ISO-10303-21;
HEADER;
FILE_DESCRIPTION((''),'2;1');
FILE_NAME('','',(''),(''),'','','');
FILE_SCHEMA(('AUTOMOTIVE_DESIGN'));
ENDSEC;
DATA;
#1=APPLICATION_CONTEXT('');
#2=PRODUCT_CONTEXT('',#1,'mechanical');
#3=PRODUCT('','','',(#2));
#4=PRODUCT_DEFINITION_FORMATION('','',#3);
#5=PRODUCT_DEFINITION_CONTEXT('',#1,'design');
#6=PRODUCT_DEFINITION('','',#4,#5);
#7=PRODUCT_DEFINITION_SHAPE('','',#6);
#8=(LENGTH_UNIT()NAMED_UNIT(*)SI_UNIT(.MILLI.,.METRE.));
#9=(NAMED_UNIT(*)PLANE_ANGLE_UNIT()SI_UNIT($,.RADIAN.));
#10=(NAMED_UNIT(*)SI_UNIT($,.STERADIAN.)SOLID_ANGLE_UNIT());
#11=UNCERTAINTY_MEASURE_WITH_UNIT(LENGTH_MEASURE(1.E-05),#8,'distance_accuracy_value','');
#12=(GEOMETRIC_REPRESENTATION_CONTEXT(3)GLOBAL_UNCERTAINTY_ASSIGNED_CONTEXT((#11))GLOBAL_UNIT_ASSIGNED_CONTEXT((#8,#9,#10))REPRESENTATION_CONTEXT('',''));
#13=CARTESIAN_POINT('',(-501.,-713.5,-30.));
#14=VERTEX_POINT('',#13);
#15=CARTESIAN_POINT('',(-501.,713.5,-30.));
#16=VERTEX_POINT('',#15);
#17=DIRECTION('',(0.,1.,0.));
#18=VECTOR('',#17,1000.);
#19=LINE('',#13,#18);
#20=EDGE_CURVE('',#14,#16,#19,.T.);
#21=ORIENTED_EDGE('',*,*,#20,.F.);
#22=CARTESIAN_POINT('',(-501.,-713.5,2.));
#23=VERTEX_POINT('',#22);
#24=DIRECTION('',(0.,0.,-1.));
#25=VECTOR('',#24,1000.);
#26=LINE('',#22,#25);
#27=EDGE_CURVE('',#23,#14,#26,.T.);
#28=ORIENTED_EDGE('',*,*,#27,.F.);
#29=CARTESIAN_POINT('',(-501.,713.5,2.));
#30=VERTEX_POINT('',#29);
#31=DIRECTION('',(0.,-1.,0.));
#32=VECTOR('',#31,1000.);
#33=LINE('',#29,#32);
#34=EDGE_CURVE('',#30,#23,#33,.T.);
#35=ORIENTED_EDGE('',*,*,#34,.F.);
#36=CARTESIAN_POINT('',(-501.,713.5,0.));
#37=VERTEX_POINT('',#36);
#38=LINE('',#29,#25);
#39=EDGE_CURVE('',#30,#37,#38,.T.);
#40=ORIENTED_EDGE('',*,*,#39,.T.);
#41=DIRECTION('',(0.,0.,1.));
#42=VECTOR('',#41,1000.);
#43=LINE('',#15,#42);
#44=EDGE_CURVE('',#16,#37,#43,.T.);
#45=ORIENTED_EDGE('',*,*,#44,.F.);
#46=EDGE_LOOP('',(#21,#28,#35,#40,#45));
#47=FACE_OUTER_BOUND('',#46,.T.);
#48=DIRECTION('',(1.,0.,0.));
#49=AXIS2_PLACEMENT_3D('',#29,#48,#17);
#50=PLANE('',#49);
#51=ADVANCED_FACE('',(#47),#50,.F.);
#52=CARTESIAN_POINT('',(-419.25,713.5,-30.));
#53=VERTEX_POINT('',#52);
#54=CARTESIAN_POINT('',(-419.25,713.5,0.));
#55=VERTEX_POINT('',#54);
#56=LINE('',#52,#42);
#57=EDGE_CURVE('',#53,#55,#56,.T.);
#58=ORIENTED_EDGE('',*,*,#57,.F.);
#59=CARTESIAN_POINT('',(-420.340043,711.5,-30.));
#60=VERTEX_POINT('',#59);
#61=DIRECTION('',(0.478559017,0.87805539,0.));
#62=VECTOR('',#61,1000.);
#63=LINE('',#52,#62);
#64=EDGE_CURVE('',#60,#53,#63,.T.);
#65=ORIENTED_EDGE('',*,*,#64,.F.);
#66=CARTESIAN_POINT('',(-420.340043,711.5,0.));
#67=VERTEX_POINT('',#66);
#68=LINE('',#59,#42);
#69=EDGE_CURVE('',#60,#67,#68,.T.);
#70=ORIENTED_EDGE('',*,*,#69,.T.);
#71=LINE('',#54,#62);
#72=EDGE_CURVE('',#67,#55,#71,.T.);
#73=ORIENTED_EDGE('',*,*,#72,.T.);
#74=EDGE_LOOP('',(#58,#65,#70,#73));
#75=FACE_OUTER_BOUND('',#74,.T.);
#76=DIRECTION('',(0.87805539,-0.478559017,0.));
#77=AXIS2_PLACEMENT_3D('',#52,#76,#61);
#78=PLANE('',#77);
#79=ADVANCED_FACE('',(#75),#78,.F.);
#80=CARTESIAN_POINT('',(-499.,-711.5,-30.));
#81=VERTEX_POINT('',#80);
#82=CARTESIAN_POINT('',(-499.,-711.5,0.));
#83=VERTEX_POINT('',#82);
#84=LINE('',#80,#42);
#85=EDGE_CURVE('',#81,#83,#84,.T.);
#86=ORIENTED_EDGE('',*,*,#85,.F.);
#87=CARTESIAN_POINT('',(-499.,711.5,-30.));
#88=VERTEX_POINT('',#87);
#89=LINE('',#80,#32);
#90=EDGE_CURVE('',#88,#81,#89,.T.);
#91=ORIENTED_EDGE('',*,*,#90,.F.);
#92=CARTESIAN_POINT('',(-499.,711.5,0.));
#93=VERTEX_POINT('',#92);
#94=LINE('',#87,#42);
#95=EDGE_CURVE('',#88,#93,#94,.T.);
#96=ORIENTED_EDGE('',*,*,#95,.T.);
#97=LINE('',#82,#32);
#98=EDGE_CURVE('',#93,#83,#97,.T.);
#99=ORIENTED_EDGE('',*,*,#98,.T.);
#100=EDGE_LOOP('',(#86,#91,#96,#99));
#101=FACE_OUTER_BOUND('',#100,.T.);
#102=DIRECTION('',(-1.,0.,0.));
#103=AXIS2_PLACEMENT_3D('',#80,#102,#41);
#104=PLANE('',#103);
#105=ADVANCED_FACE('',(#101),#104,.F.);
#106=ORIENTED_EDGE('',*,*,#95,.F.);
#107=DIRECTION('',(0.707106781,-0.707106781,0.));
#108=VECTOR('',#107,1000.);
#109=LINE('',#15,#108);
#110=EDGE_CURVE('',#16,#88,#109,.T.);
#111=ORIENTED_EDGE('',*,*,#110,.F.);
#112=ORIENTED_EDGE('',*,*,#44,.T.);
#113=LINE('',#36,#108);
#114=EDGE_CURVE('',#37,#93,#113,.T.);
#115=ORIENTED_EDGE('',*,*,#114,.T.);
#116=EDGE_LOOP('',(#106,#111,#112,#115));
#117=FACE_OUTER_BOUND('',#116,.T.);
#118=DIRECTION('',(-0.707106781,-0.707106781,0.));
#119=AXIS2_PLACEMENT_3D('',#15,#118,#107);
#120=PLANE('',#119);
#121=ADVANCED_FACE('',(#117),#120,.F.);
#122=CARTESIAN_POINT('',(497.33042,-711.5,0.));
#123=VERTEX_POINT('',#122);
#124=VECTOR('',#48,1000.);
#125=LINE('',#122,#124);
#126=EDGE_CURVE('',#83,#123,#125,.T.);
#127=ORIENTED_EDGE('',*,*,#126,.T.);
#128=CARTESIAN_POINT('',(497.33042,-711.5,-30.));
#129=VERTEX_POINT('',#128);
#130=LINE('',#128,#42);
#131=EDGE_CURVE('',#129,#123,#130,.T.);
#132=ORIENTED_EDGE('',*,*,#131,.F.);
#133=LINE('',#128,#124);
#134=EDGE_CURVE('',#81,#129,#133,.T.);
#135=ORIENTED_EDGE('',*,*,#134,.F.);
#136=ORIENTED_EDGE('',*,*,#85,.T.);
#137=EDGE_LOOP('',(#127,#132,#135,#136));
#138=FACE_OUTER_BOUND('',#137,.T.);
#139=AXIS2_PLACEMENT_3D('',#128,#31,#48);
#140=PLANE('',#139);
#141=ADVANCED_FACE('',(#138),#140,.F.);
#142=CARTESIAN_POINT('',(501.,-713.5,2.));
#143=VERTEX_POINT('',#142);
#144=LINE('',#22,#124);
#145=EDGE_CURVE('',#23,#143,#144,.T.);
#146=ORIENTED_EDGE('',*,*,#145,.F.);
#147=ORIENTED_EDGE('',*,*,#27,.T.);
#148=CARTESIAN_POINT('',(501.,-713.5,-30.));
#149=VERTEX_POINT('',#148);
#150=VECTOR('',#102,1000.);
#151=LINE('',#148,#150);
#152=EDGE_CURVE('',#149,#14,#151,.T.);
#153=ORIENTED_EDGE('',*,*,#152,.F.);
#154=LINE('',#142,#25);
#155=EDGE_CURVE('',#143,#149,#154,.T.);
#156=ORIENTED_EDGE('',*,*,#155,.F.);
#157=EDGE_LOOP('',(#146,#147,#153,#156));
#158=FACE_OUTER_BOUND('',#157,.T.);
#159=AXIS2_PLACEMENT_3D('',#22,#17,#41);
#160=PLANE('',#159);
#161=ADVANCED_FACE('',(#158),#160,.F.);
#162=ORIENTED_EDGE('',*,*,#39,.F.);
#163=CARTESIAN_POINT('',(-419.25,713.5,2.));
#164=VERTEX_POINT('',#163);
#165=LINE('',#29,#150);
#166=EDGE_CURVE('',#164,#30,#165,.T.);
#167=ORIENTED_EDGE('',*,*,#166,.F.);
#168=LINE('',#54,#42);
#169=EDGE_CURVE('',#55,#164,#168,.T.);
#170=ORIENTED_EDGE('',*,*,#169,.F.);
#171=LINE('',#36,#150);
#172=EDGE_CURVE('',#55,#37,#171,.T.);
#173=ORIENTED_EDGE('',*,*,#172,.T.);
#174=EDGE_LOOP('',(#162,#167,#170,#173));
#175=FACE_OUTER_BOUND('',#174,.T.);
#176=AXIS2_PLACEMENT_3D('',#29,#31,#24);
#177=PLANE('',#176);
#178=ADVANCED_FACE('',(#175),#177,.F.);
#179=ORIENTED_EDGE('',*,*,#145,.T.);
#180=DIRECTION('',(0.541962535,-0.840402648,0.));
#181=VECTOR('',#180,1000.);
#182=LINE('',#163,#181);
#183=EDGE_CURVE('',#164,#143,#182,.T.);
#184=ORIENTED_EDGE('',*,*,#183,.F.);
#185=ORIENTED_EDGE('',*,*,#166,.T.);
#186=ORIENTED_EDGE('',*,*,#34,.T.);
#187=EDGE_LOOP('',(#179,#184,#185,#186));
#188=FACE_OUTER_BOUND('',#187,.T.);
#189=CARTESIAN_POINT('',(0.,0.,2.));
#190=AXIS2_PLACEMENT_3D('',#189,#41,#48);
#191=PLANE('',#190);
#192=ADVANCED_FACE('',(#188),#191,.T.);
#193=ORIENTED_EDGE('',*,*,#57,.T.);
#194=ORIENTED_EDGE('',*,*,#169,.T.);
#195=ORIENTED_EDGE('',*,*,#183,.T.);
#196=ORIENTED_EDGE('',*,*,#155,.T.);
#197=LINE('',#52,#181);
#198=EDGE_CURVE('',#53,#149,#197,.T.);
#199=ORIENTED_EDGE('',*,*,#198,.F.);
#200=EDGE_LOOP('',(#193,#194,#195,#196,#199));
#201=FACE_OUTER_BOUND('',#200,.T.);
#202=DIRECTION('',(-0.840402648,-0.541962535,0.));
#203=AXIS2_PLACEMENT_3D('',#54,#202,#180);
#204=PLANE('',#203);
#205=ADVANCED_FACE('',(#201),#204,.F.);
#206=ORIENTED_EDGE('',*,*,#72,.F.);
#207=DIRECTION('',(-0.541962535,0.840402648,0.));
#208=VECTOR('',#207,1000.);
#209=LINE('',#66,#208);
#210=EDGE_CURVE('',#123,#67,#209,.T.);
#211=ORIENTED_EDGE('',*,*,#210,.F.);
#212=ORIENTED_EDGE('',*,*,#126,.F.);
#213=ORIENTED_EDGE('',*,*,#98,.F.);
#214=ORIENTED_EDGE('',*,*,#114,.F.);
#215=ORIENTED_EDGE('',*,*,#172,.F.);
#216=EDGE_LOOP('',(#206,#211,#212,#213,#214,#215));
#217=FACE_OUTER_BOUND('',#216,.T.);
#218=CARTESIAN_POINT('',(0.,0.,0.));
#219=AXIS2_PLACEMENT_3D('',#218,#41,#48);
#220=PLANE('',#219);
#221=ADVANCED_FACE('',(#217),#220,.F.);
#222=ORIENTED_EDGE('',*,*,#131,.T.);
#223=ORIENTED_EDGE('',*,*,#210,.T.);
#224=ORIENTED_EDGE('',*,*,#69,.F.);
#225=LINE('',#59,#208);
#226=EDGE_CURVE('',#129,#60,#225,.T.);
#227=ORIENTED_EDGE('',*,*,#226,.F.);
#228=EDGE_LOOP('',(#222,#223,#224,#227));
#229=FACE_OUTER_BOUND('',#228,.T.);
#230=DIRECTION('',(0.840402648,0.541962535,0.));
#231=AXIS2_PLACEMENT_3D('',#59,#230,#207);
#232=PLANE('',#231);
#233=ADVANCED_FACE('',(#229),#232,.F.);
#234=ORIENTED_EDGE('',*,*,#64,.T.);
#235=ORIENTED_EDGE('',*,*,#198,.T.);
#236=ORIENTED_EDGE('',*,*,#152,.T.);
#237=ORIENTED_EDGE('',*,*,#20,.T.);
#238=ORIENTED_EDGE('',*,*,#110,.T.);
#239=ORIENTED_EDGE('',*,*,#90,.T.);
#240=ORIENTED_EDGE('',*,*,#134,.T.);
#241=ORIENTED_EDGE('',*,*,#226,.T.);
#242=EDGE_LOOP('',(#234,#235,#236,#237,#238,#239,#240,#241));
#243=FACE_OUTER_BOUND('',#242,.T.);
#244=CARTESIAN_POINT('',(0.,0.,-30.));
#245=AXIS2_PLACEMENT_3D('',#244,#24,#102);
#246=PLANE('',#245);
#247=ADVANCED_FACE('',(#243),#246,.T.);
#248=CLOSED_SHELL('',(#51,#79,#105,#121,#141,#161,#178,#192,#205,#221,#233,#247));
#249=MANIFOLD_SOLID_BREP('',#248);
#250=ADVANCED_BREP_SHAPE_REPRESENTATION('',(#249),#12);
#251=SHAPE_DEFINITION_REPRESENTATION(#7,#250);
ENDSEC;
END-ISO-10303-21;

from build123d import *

# Parameters (mm, degrees)
SKETCH1_W           = 1002
SKETCH1_H           = 1427
BOSS_EXTRUDE1_DEPTH = 2
CUT_EXTRUDE1_DEPTH  = 2
BOSS_EXTRUDE2_DEPTH = 30


with BuildPart() as part:
    # Sketch1 → Boss-Extrude1 (new body)
    with BuildSketch(Plane.XY):
        Rectangle(SKETCH1_W, SKETCH1_H)
    extrude(amount=BOSS_EXTRUDE1_DEPTH)

    # Sketch2 → Cut-Extrude1 (cut)
    with BuildSketch(Plane.XY.offset(2)):
        Polygon((-419.25, 713.5), (501, -713.5), (501, 713.5), align=None)
    extrude(amount=-CUT_EXTRUDE1_DEPTH, mode=Mode.SUBTRACT)

    # Sketch4 → Boss-Extrude2 (add)
    with BuildSketch(Plane(origin=(0, 0, 0), x_dir=(-1, 0, 0), z_dir=(0, 0, -1))):
        Polygon((420.340042889, 711.5), (-497.33041962, -711.5), (499, -711.5), (499, 711.5), (501, 713.5), (501, -713.5), (-501, -713.5), (419.25, 713.5), align=None)
    extrude(amount=BOSS_EXTRUDE2_DEPTH)


solid = part.part
